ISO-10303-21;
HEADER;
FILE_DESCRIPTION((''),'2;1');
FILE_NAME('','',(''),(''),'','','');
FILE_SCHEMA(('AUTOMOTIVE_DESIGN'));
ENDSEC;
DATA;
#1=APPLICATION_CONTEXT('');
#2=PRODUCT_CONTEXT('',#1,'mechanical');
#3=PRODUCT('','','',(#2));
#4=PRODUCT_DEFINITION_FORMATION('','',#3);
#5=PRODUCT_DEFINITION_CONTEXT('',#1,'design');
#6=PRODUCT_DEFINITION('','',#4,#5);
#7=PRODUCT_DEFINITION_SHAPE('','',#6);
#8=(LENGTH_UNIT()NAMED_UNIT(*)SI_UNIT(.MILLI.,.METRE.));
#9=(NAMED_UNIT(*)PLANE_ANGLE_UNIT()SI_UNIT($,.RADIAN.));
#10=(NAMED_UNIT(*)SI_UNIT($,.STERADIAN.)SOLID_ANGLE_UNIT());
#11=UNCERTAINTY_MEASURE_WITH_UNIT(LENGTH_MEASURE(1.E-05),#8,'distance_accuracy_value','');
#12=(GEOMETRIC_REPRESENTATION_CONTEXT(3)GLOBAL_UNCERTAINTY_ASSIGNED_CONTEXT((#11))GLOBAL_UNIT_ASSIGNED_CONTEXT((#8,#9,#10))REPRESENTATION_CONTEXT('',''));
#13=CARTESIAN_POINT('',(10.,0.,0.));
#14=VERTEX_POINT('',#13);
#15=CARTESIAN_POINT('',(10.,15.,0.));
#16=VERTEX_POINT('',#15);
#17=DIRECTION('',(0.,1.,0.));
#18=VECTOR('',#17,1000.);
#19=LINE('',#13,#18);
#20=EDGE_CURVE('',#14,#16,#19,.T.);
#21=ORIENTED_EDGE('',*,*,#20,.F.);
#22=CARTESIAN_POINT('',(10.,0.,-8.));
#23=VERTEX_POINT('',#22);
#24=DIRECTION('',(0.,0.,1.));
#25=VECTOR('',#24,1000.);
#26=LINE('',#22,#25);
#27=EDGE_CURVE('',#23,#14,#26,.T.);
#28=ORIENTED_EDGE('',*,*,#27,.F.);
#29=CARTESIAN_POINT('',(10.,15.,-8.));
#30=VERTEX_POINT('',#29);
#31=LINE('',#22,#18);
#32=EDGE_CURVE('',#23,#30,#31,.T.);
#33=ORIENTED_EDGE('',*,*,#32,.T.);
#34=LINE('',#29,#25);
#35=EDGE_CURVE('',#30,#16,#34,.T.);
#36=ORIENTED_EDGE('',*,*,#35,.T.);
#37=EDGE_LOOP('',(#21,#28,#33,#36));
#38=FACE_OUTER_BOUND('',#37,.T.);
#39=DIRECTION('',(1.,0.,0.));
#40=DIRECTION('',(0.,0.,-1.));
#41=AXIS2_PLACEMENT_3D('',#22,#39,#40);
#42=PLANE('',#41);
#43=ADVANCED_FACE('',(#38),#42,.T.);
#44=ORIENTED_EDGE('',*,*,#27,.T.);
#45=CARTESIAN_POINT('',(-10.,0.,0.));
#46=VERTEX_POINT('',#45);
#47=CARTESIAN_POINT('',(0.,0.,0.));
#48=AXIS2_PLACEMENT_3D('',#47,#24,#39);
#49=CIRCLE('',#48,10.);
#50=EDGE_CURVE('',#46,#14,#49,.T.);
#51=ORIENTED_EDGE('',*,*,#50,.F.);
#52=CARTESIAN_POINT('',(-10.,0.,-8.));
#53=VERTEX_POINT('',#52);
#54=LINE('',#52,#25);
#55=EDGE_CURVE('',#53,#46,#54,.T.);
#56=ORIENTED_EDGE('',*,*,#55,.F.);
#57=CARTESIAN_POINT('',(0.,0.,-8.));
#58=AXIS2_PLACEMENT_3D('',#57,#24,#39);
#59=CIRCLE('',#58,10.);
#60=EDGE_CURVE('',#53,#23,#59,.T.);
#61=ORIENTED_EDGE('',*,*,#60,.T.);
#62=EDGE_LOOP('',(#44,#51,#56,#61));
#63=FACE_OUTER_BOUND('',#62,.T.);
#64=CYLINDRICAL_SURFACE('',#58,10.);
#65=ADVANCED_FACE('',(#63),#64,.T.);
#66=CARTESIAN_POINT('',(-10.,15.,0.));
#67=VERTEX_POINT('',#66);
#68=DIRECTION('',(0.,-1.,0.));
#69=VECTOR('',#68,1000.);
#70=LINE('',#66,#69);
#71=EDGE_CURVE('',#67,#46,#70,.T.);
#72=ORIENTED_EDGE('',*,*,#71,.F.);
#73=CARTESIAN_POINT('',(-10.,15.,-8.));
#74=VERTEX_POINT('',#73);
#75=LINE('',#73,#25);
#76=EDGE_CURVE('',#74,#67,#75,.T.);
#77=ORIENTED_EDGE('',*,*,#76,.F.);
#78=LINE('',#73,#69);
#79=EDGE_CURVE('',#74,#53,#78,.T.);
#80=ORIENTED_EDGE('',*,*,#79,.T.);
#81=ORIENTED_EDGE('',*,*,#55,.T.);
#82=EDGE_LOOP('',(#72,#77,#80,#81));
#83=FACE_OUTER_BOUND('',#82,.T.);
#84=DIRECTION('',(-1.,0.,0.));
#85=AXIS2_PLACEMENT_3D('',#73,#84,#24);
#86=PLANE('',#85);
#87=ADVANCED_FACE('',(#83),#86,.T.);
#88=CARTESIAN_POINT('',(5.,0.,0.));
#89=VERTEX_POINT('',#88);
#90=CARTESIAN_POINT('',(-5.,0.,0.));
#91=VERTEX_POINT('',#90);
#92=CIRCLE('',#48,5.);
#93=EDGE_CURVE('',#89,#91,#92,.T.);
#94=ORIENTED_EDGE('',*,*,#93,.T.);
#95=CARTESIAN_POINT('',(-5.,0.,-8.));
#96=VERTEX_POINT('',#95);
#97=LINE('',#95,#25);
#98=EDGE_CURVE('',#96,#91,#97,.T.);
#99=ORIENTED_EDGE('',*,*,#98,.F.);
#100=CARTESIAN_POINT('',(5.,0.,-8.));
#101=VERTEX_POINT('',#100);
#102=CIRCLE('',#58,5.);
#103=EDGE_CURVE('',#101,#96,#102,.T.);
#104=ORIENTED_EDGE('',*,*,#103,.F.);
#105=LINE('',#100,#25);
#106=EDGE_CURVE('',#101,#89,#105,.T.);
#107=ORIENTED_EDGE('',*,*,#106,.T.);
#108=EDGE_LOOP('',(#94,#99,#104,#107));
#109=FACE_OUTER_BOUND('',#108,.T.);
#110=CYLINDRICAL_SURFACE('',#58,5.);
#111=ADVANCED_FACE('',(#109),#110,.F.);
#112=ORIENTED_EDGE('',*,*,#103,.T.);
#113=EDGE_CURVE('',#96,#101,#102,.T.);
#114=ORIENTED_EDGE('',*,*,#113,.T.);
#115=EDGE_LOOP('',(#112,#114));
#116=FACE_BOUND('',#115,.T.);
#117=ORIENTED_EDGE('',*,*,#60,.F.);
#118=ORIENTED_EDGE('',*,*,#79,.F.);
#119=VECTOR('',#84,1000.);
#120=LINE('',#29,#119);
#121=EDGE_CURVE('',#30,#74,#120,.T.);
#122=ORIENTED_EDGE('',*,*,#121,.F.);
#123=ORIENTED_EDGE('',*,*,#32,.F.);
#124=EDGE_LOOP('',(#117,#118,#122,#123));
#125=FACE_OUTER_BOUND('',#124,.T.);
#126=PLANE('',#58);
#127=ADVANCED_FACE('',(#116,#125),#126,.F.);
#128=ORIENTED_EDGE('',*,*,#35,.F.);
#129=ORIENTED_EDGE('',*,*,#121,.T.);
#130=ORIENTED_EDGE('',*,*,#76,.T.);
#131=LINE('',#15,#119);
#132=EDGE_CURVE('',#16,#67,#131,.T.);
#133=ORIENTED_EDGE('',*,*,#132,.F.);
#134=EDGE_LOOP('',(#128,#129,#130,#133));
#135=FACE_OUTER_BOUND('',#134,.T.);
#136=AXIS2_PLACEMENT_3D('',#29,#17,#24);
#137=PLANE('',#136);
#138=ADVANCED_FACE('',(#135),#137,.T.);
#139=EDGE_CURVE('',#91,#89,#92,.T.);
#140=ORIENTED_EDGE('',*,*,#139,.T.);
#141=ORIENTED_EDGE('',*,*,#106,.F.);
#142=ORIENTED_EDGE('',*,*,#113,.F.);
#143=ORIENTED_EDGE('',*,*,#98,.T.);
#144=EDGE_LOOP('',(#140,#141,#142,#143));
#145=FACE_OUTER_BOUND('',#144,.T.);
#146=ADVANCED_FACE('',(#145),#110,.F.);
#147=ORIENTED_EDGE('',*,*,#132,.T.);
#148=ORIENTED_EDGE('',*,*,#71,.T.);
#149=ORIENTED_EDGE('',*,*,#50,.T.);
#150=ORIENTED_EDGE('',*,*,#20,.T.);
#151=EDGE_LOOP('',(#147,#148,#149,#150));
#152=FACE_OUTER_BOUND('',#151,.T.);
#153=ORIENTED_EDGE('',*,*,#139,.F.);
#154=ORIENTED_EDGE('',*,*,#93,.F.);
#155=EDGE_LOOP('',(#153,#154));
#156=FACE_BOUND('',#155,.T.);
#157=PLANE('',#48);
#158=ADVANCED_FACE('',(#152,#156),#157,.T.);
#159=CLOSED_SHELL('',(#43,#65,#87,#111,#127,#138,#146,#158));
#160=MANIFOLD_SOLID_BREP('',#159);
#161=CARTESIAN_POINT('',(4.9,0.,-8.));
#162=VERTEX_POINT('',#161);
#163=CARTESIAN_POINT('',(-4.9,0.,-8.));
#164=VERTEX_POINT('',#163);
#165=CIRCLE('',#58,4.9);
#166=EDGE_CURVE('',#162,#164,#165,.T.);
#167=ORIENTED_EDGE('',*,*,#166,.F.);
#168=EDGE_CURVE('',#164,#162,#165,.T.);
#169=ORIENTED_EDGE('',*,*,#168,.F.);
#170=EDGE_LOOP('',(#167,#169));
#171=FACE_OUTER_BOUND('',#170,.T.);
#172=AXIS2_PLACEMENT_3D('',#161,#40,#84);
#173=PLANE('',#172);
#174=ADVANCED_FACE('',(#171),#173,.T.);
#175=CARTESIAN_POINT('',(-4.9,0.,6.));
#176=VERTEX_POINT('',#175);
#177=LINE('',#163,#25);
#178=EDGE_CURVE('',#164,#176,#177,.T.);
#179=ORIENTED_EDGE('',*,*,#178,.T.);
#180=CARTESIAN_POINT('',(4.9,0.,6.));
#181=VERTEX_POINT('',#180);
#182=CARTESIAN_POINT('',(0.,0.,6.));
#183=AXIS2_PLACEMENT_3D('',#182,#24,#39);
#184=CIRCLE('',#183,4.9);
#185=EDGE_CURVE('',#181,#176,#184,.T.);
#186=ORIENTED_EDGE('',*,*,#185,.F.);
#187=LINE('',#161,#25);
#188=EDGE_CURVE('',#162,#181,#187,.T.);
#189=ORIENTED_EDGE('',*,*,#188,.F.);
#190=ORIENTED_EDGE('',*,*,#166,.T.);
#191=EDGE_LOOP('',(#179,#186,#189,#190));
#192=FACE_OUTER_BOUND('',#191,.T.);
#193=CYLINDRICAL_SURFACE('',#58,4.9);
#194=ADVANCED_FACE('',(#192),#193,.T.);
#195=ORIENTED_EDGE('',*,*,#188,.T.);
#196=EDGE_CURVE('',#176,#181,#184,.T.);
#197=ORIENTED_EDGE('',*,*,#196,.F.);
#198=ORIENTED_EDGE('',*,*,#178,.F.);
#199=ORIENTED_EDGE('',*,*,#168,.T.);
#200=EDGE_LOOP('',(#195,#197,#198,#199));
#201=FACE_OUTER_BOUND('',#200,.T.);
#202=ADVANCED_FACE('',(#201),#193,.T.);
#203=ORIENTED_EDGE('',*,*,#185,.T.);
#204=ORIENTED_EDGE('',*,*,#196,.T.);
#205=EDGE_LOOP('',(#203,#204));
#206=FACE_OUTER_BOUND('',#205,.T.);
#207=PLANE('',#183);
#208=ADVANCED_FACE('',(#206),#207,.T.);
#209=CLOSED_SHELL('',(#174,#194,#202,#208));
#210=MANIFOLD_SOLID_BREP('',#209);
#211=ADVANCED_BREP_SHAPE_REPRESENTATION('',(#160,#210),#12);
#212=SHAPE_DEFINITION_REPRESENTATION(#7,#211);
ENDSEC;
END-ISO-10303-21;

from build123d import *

# Parameters (mm, degrees)
SKETCH3_R           = 5
BOSS_EXTRUDE1_DEPTH = 8
SKETCH6_W           = 4.9
SKETCH6_H           = 14


with BuildPart() as part:
    # Sketch3 → Boss-Extrude1 (new body)
    with BuildSketch(Plane.XY):
        with BuildLine():
            Line((10, 0), (10, 15))
            Line((10, 15), (-10, 15))
            Line((-10, 15), (-10, 0))
            ThreePointArc((-10, 0), (0, -10), (10, 0))
        make_face()
        Circle(SKETCH3_R, mode=Mode.SUBTRACT)
    extrude(amount=-BOSS_EXTRUDE1_DEPTH)


with BuildPart() as body_2:
    # Sketch6 → Revolve2 (revolve)
    with BuildSketch(Plane(origin=(0, 0, 0), x_dir=(1, 0, 0), z_dir=(0, 1, 0))):
        with Locations((2.45, 1)):
            Rectangle(SKETCH6_W, SKETCH6_H)
    revolve(axis=Axis((0, 0, -8), (0, 0, 1)))


solid = Compound([part.part, body_2.part])
